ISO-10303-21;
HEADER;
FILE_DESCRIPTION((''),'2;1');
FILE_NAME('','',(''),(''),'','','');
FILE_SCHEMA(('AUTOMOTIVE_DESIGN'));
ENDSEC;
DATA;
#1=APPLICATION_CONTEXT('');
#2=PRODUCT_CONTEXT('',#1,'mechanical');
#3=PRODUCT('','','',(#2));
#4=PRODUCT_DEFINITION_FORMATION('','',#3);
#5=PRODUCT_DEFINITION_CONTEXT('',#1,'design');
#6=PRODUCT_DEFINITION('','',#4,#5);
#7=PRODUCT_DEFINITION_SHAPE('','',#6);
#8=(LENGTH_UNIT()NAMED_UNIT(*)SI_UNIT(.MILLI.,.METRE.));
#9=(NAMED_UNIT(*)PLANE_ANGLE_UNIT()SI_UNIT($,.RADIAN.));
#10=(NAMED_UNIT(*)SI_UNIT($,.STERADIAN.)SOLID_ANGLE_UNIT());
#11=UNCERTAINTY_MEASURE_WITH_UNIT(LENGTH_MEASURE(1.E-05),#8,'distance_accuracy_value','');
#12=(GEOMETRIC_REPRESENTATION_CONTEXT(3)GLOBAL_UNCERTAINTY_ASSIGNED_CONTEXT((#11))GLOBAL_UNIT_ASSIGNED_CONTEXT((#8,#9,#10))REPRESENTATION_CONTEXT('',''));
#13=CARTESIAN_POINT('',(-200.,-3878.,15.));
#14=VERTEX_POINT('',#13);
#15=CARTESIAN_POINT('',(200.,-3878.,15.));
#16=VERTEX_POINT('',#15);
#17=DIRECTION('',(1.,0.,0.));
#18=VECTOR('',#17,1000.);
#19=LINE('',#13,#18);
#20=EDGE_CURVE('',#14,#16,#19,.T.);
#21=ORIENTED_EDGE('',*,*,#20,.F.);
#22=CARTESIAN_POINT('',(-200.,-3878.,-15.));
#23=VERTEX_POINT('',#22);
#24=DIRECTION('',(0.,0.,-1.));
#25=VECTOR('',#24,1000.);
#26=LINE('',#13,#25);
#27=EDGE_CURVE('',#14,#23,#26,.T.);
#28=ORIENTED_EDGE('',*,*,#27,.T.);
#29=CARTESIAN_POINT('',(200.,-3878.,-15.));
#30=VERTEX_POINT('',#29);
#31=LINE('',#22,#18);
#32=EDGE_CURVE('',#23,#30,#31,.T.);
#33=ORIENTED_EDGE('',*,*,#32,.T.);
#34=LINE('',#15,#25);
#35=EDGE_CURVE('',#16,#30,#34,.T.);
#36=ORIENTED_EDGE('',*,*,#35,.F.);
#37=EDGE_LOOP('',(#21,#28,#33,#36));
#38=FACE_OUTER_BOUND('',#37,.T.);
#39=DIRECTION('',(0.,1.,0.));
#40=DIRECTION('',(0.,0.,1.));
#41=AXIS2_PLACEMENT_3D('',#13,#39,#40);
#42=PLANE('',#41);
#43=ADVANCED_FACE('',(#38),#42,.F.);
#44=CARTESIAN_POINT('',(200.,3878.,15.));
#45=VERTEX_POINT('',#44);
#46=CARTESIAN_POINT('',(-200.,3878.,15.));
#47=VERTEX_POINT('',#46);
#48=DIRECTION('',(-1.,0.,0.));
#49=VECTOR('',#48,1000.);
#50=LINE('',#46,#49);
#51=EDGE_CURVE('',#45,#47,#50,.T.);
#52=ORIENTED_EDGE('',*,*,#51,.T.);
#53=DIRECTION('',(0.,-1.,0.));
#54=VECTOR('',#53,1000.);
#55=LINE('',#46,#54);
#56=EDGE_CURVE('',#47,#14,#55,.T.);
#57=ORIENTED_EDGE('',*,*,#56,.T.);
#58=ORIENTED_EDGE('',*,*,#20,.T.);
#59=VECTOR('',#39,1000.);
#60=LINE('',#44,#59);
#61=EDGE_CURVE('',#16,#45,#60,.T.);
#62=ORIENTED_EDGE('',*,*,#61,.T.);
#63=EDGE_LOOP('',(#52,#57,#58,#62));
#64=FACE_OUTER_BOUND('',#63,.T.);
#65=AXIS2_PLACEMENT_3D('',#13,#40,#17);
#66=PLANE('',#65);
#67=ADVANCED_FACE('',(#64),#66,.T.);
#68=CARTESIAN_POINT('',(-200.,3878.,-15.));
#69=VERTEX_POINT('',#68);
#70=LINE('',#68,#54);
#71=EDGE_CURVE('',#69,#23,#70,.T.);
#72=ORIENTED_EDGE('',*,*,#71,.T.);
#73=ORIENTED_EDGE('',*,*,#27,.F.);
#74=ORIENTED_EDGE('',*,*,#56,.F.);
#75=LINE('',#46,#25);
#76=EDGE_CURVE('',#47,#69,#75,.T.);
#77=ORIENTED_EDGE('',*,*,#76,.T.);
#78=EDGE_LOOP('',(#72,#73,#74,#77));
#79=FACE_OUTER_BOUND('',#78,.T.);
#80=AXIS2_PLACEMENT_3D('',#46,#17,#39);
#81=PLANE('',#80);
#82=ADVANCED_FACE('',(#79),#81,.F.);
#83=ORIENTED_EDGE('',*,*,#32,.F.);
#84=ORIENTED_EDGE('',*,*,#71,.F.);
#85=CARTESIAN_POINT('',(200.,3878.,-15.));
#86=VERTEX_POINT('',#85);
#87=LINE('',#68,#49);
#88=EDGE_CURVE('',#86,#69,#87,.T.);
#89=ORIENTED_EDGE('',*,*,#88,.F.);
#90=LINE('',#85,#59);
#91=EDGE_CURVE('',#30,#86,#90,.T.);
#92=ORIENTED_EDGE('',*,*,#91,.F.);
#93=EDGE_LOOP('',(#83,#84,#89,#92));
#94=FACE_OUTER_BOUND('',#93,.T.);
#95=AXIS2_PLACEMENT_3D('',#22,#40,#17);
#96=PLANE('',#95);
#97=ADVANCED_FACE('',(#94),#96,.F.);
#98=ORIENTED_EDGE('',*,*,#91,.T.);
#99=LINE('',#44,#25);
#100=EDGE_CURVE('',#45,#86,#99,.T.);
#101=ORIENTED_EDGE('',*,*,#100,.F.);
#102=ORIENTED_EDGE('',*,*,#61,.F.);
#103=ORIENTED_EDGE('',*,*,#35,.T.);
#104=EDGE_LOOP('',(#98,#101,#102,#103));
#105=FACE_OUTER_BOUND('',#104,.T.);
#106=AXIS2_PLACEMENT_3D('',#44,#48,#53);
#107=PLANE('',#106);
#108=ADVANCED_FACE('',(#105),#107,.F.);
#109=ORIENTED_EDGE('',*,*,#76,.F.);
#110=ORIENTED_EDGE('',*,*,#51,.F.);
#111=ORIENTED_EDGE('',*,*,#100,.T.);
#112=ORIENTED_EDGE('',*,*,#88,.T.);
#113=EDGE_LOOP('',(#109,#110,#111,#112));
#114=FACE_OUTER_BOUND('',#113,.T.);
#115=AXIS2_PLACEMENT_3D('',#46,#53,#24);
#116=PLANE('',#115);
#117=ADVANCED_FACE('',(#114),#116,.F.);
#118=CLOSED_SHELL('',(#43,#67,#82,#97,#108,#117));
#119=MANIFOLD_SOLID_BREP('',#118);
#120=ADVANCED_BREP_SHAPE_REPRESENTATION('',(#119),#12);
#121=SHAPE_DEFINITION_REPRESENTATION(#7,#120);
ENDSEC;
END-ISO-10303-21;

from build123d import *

# Parameters (mm, degrees)
SKETCH1_W           = 400
SKETCH1_H           = 7756
BOSS_EXTRUDE1_DEPTH = 15


with BuildPart() as part:
    # Sketch1 → Boss-Extrude1 (new, symmetric)
    with BuildSketch(Plane.XY):
        Rectangle(SKETCH1_W, SKETCH1_H)
    extrude(amount=BOSS_EXTRUDE1_DEPTH, both=True)


solid = part.part
